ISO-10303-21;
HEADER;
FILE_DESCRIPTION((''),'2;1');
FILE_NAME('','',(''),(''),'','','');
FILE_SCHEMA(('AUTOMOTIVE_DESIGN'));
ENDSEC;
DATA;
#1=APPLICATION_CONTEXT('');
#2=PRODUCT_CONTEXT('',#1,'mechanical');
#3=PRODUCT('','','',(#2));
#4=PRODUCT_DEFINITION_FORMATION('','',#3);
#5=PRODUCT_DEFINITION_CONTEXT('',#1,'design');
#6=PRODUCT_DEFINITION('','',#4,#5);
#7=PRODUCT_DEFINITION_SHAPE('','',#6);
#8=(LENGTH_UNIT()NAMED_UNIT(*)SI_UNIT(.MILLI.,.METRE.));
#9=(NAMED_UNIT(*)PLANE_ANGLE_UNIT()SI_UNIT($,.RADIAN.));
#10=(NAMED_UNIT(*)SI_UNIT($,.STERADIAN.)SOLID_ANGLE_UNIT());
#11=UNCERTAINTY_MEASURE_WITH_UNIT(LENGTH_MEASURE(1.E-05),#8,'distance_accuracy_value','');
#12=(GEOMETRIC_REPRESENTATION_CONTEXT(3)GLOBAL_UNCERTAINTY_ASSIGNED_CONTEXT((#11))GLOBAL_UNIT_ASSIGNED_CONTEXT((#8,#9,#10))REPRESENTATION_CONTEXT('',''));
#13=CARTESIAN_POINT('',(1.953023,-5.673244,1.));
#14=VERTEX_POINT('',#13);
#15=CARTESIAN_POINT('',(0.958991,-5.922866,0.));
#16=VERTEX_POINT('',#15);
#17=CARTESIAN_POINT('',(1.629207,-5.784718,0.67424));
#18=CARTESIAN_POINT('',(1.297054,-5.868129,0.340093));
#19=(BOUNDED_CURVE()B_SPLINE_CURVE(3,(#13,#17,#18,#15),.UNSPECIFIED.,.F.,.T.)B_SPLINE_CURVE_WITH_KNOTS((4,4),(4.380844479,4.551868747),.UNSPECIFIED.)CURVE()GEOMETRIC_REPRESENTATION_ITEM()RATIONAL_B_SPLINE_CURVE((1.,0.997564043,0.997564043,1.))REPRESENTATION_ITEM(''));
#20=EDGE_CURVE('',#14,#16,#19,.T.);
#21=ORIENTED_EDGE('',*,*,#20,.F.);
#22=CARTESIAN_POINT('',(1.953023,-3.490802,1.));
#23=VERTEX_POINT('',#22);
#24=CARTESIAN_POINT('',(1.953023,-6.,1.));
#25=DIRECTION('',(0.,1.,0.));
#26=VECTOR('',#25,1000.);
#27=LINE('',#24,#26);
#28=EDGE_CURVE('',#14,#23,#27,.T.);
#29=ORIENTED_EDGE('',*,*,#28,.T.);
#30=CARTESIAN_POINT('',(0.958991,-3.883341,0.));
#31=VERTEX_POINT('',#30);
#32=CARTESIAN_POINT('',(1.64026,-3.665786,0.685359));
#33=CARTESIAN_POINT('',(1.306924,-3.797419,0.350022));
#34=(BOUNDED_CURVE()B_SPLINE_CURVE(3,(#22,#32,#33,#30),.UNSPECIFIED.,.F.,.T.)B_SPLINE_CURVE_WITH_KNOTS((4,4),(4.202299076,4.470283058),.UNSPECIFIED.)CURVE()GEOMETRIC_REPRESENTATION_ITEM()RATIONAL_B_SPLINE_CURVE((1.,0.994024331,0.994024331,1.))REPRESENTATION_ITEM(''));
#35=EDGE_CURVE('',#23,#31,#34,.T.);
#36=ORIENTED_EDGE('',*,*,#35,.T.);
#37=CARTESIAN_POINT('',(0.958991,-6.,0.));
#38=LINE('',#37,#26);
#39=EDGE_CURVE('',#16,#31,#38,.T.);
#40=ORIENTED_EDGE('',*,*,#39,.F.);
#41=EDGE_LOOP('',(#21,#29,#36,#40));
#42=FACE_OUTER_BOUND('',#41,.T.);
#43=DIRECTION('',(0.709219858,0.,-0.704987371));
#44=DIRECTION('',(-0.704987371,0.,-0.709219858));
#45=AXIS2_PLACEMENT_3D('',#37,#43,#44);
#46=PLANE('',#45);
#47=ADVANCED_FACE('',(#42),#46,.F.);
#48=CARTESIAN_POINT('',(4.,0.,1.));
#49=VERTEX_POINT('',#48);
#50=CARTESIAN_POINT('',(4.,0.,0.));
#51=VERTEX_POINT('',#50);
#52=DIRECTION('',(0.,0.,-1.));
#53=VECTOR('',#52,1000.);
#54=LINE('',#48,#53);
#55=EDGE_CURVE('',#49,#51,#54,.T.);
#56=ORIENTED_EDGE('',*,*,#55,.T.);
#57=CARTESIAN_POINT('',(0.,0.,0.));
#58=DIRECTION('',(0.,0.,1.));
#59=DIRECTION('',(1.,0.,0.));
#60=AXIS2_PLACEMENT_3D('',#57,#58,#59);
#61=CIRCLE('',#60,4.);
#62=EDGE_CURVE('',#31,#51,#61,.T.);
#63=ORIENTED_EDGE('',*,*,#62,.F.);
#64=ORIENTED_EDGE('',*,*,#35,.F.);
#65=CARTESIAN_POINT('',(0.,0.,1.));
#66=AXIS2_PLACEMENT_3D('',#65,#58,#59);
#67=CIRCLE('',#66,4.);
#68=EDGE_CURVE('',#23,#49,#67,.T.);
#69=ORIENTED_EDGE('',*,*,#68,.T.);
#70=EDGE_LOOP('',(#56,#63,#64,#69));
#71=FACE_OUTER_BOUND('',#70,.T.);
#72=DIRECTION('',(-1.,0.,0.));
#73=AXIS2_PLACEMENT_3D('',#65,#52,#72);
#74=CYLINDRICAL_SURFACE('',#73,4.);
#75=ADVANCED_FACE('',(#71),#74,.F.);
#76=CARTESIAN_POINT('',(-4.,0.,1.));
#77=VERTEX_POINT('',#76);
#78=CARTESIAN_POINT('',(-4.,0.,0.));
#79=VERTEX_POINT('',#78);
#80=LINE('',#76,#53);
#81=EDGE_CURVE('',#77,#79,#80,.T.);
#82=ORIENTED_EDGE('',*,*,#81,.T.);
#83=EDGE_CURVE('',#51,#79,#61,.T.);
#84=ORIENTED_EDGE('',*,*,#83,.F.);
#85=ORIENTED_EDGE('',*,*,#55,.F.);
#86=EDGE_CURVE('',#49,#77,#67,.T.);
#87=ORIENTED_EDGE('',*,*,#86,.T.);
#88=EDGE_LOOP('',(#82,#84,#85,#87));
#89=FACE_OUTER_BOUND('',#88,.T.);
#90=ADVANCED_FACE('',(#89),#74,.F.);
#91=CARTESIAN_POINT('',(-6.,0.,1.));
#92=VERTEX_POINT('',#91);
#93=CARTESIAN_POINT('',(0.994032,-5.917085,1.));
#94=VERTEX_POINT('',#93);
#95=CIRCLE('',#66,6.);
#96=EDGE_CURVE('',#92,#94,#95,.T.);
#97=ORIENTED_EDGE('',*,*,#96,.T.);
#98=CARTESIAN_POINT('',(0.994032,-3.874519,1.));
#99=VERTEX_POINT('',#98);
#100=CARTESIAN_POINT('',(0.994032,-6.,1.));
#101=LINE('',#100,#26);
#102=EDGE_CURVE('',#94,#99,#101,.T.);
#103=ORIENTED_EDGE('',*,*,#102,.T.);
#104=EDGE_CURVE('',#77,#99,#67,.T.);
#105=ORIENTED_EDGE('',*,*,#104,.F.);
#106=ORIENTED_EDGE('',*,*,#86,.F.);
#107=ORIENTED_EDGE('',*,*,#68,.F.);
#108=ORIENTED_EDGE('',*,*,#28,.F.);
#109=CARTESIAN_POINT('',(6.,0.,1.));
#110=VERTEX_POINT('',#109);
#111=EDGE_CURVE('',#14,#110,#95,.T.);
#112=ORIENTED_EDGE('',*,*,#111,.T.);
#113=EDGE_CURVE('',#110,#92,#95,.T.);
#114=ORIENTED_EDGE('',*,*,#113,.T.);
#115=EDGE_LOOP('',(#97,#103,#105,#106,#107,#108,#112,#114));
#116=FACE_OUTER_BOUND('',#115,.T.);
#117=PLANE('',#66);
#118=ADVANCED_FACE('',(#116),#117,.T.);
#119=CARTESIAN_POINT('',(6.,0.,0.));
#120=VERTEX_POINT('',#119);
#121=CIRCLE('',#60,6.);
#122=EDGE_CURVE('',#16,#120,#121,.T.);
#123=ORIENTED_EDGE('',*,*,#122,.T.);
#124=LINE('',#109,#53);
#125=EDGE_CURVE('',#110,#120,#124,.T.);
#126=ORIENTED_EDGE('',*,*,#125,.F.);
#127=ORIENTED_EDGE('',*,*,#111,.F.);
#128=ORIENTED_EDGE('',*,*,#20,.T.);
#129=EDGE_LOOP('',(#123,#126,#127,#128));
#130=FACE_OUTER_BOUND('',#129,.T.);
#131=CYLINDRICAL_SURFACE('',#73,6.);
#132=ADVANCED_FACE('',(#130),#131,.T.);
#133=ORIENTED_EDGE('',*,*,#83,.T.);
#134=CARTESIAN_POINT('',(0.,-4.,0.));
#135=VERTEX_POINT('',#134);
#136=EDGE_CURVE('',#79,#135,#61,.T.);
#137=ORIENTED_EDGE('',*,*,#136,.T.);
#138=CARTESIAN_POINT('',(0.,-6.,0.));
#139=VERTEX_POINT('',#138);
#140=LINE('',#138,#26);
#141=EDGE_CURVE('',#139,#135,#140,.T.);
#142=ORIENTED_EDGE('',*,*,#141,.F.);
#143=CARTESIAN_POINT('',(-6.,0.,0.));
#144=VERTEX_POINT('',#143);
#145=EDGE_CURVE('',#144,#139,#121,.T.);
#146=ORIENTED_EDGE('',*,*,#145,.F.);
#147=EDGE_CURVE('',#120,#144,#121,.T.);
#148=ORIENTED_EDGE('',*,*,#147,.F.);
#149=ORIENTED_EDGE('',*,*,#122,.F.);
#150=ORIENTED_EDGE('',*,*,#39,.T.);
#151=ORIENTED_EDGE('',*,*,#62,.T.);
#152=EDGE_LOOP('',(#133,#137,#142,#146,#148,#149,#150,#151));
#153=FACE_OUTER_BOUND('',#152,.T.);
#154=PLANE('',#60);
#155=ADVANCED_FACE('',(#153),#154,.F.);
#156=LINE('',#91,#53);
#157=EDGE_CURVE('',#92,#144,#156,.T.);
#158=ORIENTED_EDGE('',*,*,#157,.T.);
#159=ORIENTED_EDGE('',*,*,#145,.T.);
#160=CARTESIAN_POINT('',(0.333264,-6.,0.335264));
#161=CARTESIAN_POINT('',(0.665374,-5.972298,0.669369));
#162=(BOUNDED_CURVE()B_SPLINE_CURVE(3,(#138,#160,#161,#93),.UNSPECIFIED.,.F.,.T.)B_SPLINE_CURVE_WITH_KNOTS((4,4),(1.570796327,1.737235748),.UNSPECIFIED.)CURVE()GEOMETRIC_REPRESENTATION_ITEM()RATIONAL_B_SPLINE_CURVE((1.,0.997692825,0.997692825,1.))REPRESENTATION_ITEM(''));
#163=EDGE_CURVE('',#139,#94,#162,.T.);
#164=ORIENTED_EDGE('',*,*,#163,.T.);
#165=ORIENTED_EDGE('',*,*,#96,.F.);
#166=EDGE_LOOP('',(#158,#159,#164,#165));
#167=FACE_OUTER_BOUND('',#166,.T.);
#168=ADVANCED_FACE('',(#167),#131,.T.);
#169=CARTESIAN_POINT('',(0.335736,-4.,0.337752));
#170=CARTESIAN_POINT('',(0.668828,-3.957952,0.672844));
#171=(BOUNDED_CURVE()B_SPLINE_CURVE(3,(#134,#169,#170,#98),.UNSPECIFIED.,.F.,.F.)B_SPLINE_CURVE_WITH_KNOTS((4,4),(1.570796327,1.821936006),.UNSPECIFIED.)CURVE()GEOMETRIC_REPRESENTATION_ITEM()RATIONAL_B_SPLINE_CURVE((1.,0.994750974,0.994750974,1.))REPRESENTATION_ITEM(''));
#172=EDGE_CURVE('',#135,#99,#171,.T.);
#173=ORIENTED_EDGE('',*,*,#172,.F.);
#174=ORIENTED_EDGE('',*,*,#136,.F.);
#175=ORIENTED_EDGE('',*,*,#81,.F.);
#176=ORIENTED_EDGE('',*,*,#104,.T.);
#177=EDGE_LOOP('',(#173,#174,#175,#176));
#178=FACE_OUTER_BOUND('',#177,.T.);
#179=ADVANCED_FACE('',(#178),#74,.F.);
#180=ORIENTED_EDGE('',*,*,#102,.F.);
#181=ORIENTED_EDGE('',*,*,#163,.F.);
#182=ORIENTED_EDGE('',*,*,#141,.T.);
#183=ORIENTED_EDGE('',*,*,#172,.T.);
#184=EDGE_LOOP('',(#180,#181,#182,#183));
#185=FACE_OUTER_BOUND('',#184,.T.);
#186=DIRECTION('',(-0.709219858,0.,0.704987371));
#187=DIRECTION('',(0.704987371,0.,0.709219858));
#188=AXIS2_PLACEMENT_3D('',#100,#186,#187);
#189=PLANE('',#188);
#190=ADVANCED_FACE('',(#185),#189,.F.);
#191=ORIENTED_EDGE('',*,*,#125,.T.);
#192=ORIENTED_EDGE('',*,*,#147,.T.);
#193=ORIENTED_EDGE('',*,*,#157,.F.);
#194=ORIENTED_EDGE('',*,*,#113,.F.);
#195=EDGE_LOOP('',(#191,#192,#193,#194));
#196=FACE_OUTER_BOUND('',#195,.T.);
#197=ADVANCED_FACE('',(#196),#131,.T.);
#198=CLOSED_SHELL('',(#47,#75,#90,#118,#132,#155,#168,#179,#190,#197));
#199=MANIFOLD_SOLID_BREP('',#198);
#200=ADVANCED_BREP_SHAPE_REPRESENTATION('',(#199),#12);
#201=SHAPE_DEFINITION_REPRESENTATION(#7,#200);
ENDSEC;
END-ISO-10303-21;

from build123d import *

# Parameters (mm, degrees)
SKETCH1_R           = 6
SKETCH1_R_2         = 4
BOSS_EXTRUDE1_DEPTH = 1
CUT_EXTRUDE1_DEPTH  = 9.544003745


with BuildPart() as part:
    # Sketch1 → Boss-Extrude1 (new body)
    with BuildSketch(Plane.XY):
        Circle(SKETCH1_R)
        Circle(SKETCH1_R_2, mode=Mode.SUBTRACT)
    extrude(amount=BOSS_EXTRUDE1_DEPTH)

    # Sketch2 → Cut-Extrude1 (cut, through all)
    with BuildSketch(Plane(origin=(0, 0, 0), x_dir=(1, 0, 0), z_dir=(0, 1, 0))):
        Polygon((0, 0), (0.95899064, 0), (1.953022833, -1), (0.994032193, -1), align=None)
    extrude(amount=-CUT_EXTRUDE1_DEPTH, mode=Mode.SUBTRACT)


solid = part.part
